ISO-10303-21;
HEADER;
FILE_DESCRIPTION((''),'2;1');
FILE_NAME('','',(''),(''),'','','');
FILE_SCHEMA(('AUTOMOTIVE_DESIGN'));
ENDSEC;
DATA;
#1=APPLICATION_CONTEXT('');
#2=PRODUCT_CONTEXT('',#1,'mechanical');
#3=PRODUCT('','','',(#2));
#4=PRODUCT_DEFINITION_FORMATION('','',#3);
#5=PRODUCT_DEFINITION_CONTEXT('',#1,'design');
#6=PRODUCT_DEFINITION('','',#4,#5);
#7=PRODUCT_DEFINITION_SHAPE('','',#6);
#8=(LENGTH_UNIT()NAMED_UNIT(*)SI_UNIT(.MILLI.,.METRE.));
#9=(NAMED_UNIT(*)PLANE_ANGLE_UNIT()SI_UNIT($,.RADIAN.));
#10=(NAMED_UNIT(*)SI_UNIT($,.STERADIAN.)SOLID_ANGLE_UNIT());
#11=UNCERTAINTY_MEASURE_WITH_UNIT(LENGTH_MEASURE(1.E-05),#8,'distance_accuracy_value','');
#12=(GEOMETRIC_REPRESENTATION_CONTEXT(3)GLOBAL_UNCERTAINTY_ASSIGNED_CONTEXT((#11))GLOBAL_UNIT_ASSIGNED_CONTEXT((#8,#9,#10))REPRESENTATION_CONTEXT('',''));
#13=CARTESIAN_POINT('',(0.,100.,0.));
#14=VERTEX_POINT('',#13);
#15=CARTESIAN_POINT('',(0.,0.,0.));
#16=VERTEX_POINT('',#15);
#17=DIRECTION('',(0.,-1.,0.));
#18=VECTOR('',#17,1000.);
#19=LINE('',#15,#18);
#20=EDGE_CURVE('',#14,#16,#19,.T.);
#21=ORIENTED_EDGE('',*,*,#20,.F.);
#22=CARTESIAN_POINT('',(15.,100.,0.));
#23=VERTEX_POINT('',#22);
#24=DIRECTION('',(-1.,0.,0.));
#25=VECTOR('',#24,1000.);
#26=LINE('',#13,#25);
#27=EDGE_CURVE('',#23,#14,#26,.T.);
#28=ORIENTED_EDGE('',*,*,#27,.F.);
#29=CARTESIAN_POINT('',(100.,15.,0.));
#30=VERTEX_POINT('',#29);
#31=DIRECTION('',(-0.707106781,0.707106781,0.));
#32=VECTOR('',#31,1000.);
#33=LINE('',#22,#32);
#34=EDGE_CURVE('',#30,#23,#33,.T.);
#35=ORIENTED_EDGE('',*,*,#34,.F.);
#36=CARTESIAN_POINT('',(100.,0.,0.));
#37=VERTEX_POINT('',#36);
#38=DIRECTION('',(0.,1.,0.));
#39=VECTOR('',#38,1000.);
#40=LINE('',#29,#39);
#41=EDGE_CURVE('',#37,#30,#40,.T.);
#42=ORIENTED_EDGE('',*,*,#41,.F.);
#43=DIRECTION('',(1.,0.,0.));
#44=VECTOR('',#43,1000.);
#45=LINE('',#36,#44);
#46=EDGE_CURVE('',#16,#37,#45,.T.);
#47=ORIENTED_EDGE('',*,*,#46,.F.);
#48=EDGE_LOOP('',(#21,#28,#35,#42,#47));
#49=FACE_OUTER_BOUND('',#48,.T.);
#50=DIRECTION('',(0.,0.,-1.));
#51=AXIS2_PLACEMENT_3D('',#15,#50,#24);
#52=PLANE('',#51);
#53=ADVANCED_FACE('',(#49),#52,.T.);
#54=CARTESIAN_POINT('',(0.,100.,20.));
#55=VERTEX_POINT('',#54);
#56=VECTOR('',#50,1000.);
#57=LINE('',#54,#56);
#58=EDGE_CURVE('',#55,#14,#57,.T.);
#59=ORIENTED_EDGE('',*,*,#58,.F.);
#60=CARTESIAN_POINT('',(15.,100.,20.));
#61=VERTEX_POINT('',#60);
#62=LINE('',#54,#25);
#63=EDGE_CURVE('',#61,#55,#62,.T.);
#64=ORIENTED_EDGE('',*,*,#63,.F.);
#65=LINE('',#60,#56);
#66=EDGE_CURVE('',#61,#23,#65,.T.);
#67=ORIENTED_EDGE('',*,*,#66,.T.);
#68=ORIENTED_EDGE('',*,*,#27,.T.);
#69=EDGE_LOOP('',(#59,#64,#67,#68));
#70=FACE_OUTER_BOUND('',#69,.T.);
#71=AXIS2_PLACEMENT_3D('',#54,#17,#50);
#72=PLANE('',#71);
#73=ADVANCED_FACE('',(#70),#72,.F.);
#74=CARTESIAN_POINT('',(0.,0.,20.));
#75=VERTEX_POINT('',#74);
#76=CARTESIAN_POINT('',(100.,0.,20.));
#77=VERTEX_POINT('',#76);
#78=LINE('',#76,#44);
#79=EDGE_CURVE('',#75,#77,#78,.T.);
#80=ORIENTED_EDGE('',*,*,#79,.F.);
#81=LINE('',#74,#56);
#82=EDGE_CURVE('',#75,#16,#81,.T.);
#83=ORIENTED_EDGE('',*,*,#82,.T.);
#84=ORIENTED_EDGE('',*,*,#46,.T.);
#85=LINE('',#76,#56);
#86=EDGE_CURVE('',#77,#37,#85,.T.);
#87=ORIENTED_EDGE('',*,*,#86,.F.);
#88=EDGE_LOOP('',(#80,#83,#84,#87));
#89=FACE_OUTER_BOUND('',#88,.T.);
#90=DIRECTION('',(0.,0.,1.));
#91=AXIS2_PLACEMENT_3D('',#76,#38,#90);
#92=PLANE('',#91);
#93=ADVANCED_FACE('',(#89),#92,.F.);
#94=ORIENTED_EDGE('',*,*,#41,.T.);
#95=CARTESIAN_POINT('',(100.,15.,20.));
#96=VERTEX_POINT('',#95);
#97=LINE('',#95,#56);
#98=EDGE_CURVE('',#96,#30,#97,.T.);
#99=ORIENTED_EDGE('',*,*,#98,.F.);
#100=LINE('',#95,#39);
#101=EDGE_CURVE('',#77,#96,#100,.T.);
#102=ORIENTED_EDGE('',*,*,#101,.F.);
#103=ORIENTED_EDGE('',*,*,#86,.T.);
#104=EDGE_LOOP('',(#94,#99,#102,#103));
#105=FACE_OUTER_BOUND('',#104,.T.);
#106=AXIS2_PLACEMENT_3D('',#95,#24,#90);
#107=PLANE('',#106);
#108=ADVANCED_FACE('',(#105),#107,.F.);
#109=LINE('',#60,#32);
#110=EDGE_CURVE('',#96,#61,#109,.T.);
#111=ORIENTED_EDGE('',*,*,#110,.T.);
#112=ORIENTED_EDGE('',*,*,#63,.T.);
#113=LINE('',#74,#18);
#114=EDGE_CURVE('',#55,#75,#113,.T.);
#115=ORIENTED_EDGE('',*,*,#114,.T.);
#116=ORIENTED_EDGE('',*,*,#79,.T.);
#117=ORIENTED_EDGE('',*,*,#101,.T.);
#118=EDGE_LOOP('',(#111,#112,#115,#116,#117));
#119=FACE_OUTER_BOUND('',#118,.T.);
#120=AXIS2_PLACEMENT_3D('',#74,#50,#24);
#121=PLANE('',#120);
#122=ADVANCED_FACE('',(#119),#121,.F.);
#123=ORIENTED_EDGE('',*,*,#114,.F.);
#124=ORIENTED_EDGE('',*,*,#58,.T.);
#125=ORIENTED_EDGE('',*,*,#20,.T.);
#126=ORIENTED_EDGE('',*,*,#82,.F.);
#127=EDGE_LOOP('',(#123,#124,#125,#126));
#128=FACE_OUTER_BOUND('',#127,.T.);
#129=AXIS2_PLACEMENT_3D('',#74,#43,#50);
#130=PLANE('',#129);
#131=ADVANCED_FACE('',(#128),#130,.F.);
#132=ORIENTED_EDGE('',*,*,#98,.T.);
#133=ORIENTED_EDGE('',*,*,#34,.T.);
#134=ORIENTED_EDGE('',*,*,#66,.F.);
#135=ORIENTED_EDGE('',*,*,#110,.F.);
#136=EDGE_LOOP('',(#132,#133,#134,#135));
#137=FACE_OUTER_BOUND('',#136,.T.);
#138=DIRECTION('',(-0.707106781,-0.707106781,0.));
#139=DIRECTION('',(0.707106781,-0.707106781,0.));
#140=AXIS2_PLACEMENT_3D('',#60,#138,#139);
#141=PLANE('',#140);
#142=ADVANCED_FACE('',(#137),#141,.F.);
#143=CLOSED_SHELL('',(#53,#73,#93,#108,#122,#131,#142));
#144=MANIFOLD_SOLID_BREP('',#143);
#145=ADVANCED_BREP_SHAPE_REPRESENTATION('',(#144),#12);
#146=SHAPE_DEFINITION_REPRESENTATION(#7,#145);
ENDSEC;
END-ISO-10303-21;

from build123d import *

# Parameters (mm, degrees)
BOSS_EXTRUDE1_DEPTH = 20


with BuildPart() as part:
    # Sketch1 → Boss-Extrude1 (new body)
    with BuildSketch(Plane.XY):
        Polygon((0, 0), (0, 100), (15, 100), (100, 15), (100, 0), align=None)
    extrude(amount=BOSS_EXTRUDE1_DEPTH)


solid = part.part
